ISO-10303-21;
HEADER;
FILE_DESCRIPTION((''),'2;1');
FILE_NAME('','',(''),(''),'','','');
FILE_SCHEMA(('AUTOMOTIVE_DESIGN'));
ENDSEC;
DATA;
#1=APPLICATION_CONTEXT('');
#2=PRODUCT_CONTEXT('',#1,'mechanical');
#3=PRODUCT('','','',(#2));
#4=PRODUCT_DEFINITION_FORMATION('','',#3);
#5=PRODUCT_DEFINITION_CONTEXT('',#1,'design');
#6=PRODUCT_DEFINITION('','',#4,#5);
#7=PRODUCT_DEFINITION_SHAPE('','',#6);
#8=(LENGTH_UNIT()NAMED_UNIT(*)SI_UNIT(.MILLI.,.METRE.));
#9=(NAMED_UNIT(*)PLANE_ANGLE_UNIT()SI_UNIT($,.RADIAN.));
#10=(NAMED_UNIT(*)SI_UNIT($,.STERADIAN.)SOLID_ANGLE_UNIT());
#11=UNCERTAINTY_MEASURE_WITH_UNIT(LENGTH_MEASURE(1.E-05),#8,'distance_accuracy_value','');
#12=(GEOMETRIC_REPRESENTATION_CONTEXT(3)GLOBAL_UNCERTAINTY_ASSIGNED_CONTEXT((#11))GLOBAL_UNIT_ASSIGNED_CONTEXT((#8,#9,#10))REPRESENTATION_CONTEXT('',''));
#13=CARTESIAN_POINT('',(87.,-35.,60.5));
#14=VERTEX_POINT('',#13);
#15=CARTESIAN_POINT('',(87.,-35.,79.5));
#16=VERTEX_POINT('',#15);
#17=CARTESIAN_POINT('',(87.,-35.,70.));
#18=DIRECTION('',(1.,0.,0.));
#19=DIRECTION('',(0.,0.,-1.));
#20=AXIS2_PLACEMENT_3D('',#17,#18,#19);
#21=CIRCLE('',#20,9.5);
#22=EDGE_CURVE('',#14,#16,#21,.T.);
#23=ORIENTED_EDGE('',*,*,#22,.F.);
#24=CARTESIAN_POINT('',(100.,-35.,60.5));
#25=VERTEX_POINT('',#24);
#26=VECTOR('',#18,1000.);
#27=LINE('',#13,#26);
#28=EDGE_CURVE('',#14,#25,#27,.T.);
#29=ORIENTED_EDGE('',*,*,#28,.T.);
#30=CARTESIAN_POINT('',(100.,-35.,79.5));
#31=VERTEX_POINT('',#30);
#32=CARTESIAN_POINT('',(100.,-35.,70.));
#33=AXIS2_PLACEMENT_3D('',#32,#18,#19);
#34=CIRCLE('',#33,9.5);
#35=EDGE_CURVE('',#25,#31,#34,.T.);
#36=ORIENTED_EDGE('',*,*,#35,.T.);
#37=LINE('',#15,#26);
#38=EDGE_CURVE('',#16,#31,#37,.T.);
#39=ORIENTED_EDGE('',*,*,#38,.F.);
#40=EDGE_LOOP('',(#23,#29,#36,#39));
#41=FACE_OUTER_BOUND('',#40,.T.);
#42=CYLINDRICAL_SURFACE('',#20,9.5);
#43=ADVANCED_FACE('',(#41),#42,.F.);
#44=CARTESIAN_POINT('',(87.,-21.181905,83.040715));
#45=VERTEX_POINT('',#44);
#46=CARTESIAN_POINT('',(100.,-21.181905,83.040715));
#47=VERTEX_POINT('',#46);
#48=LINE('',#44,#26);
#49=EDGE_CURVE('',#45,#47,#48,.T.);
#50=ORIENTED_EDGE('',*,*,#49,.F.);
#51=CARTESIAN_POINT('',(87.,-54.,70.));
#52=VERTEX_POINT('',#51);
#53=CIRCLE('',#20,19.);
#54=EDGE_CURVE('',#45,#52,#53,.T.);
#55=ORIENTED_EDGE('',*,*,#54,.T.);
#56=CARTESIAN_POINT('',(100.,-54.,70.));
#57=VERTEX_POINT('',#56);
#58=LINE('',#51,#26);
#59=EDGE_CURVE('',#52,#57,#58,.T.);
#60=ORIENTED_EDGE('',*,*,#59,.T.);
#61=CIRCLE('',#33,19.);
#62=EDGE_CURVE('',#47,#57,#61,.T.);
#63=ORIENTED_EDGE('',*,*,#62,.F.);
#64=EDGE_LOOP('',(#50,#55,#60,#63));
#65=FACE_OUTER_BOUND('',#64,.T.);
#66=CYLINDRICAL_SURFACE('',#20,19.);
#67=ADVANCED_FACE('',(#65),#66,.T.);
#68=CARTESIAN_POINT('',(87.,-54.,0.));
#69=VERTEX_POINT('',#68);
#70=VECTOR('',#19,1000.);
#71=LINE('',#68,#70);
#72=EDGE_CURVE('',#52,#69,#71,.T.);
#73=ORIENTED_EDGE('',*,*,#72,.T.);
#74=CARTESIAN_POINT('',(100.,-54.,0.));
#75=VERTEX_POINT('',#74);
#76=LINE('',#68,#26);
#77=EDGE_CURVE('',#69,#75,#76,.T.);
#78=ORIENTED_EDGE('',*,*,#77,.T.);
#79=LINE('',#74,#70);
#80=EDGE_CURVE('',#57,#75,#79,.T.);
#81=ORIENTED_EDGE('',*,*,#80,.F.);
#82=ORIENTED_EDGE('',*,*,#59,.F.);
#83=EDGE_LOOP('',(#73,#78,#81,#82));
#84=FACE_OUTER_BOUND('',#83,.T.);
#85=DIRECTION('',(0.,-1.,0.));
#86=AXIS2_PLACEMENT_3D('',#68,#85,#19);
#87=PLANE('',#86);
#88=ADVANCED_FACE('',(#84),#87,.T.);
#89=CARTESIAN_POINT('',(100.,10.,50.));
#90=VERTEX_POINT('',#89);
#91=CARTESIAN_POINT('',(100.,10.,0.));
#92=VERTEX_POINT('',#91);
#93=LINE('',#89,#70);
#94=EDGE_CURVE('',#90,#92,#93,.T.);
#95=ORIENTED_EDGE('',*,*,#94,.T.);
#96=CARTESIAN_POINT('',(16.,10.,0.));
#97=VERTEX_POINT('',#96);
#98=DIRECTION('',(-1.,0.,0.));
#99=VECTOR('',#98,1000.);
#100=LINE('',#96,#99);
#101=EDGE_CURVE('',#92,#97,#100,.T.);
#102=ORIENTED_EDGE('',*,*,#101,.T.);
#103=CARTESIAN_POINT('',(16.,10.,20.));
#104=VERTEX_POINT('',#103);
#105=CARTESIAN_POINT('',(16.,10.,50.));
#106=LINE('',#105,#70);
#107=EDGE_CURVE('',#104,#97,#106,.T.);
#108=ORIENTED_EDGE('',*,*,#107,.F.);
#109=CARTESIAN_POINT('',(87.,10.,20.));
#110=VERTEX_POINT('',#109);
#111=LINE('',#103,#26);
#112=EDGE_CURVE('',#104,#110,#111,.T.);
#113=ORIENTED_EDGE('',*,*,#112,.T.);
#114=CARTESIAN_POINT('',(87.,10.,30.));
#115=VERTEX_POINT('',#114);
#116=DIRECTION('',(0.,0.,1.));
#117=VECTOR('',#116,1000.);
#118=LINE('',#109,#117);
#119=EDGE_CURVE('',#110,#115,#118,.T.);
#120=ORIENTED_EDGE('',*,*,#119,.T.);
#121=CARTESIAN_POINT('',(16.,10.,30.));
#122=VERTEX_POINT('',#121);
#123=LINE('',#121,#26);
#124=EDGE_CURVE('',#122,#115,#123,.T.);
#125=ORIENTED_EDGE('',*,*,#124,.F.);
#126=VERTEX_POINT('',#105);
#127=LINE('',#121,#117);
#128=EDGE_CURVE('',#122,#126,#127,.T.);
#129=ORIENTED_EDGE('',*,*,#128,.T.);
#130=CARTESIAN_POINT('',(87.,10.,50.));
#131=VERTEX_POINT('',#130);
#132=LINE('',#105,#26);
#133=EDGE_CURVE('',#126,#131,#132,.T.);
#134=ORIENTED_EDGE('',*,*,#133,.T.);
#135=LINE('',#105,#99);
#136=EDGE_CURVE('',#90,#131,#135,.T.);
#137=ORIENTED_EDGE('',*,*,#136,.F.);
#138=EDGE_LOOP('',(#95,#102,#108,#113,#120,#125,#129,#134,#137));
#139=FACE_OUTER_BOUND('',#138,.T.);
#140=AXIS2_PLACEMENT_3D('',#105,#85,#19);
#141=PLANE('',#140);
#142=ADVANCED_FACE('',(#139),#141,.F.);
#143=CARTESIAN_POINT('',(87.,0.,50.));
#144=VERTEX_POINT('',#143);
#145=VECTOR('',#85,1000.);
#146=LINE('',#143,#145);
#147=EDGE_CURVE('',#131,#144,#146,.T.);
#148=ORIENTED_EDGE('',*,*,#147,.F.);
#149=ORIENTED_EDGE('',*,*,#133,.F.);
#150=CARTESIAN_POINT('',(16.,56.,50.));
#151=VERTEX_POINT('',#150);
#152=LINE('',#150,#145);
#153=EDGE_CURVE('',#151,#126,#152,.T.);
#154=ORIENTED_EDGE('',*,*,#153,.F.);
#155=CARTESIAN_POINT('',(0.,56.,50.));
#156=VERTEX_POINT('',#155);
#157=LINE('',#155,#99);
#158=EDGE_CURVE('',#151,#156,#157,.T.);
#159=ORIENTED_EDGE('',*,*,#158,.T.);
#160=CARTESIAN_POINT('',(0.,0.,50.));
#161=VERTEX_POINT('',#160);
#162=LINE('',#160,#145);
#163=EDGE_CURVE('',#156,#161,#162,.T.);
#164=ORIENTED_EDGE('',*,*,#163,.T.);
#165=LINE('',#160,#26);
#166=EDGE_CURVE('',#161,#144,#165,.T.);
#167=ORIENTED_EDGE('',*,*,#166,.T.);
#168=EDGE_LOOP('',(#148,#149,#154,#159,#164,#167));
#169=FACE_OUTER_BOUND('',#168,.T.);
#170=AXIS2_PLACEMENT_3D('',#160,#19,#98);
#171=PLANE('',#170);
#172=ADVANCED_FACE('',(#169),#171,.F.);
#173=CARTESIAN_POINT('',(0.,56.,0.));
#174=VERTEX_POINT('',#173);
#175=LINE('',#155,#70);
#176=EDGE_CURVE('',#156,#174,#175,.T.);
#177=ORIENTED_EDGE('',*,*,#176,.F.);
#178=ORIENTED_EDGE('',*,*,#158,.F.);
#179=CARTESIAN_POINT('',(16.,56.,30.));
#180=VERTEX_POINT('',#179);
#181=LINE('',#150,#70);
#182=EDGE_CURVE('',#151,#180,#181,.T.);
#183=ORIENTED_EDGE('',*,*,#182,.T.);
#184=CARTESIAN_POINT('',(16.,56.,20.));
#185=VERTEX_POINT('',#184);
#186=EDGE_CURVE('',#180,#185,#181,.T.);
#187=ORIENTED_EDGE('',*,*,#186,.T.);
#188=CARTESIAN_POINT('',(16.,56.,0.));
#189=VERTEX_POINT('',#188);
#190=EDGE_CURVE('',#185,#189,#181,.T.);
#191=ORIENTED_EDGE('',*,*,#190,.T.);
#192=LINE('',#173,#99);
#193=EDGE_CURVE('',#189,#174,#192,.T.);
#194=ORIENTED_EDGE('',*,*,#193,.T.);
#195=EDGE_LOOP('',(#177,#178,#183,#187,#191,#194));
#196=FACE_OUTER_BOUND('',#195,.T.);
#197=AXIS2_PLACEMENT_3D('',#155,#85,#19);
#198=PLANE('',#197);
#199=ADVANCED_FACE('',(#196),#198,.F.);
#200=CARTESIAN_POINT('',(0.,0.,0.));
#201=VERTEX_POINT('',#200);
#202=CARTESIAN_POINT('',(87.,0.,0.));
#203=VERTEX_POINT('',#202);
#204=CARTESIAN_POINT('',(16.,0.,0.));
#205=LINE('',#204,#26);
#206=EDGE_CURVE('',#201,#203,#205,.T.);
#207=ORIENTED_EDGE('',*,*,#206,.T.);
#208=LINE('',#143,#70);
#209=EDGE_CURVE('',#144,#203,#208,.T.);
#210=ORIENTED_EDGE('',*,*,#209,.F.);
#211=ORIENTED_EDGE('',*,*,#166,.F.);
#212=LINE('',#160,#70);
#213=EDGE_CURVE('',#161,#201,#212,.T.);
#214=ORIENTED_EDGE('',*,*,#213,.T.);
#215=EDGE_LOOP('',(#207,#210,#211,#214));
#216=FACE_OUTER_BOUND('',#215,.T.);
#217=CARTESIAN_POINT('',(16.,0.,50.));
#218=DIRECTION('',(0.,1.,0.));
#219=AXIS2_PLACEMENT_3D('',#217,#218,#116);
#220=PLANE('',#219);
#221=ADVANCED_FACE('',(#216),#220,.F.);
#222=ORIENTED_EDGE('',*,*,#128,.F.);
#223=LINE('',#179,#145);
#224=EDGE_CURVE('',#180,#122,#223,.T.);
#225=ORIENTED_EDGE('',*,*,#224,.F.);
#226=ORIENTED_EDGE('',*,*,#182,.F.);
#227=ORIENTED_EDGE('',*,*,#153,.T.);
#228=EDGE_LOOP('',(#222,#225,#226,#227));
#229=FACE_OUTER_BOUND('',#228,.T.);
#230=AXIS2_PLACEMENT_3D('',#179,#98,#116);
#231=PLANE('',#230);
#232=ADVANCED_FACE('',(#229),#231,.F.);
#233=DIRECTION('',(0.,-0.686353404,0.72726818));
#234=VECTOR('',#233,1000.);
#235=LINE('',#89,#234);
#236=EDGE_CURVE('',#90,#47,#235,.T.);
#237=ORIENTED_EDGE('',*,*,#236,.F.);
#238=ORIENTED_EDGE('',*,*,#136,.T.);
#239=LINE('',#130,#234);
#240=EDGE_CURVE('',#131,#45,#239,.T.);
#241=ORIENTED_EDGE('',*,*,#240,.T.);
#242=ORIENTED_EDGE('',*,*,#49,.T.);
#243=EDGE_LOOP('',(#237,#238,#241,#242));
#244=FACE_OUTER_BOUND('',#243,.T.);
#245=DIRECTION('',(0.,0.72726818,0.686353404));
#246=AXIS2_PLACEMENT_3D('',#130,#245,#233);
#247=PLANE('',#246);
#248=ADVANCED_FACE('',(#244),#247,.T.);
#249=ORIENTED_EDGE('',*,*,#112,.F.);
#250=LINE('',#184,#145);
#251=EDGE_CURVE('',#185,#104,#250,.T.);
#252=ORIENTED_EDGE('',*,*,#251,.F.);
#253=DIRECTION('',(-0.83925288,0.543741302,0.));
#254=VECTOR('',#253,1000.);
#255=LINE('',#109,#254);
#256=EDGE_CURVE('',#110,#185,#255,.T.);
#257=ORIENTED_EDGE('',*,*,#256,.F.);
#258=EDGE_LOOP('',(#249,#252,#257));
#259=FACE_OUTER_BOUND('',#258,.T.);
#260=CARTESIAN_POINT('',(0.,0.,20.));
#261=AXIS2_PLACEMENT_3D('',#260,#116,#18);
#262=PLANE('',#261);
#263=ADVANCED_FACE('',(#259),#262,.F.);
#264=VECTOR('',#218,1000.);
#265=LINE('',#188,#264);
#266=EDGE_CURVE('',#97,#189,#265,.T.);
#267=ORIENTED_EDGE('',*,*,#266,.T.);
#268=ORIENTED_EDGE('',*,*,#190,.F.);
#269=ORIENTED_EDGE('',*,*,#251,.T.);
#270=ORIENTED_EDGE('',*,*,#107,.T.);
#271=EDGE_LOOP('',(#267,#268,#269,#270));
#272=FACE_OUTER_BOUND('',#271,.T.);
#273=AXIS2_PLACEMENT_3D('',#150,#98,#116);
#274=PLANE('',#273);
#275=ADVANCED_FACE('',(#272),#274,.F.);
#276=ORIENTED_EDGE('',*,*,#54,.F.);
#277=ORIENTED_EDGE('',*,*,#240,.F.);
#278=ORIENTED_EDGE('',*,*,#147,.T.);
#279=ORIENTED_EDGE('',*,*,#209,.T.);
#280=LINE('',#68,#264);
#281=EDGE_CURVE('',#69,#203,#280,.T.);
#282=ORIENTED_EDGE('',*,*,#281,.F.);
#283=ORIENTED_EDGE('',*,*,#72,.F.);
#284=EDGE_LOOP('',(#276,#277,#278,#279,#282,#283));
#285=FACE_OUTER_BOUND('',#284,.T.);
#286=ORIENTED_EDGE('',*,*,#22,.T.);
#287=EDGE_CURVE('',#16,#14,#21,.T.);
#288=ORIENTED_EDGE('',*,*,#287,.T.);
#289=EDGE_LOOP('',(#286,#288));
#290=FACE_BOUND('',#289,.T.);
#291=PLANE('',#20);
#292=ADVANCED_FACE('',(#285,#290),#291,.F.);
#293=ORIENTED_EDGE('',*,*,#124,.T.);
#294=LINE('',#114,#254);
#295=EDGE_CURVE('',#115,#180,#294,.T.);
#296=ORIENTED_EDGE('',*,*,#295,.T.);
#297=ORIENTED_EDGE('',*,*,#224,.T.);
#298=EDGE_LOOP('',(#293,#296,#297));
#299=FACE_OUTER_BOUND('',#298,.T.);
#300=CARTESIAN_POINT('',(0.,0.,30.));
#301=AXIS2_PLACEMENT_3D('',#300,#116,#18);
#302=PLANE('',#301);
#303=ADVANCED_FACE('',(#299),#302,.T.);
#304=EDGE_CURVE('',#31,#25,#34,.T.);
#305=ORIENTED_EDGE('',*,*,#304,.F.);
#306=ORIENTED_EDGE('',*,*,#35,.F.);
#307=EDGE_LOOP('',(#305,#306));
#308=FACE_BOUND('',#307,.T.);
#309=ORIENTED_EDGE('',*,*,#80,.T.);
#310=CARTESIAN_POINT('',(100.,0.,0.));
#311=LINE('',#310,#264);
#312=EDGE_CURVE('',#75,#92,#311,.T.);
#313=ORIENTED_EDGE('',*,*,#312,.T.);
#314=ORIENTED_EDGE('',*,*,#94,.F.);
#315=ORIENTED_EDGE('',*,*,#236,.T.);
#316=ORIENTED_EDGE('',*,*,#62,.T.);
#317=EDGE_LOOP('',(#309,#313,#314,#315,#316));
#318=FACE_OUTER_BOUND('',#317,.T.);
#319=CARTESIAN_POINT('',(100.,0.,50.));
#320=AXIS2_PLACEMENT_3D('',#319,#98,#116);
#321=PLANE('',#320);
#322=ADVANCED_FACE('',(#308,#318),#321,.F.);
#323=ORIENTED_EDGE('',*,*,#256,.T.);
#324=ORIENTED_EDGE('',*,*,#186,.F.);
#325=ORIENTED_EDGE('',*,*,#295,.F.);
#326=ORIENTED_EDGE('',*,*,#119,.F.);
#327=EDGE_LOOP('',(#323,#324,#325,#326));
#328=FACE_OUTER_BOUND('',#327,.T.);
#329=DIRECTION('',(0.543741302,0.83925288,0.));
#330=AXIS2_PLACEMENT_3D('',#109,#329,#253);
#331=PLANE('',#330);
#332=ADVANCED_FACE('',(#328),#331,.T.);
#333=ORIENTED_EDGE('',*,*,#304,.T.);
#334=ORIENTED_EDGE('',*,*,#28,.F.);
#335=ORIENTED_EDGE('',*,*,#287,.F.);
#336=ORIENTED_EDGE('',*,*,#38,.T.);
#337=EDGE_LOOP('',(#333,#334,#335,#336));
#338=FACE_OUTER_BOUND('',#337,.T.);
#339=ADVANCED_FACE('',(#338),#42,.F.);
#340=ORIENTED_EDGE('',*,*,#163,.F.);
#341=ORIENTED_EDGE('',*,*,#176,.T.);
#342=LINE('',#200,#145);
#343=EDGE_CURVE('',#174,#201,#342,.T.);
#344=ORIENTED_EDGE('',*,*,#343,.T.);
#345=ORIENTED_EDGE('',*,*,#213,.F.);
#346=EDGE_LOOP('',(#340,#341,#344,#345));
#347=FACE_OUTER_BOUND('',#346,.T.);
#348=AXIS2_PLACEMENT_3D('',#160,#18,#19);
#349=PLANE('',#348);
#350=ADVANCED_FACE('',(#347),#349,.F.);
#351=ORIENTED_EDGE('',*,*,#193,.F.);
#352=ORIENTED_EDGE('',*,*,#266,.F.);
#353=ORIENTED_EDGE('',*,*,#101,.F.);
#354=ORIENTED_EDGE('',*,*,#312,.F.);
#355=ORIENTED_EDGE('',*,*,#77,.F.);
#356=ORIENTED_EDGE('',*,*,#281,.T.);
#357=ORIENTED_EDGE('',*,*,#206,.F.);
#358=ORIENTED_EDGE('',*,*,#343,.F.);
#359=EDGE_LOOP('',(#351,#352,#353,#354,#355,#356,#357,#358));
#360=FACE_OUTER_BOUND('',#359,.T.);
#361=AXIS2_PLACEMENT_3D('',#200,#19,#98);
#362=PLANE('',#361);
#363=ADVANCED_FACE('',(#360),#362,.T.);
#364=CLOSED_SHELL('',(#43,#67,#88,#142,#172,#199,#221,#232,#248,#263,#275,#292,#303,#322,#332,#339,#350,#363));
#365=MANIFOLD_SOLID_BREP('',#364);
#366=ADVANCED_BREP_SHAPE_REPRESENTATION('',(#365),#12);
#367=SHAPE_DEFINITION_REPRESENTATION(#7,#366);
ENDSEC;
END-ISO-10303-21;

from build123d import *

# Parameters (mm, degrees)
BASE_BRACKET_DEPTH    = 50
PIVOT_LUG_DEPTH       = 13
PIVOT_HOLE_SKETCH_R   = 9.5
PIVOT_HOLE_19_DEPTH   = 13
GUSSET_DEPTH          = 30
GUSSET_TRIM_CUT_DEPTH = 20


with BuildPart() as part:
    # Base Profile Sketch → Base Bracket (new body)
    with BuildSketch(Plane.XY):
        Polygon((0, 0), (16, 0), (100, 0), (100, 10), (16, 10), (16, 56), (0, 56), align=None)
    extrude(amount=BASE_BRACKET_DEPTH)

    # Pivot Lug Sketch → Pivot Lug (add)
    with BuildSketch(Plane(origin=(100, 0, 0), x_dir=(0, 0, -1), z_dir=(1, 0, 0))):
        with BuildLine():
            Line((0, -54), (0, 10))
            Line((0, 10), (-50, 10))
            Line((-50, 10), (-83.040714674, -21.181904589))
            ThreePointArc((-83.040714674, -21.181904589), (-87.657063924, -42.016273484), (-70, -54))
            Line((-70, -54), (0, -54))
        make_face()
    extrude(amount=-PIVOT_LUG_DEPTH)

    # Pivot Hole Sketch → Pivot Hole Ø19 (cut)
    with BuildSketch(Plane(origin=(100, 0, 0), x_dir=(0, 0, -1), z_dir=(1, 0, 0))):
        with Locations((-70, -35)):
            Circle(PIVOT_HOLE_SKETCH_R)
    extrude(amount=-PIVOT_HOLE_19_DEPTH, mode=Mode.SUBTRACT)

    # Gusset Sketch → Gusset (add)
    with BuildSketch(Plane.XY.offset(50)):
        Polygon((16, 56), (16, 10), (87, 10), align=None)
    extrude(amount=-GUSSET_DEPTH)

    # Gusset Trim Sketch → Gusset Trim Cut (cut)
    with BuildSketch(Plane.XY.offset(50)):
        Polygon((16, 56), (16, 10), (87, 10), align=None)
    extrude(amount=-GUSSET_TRIM_CUT_DEPTH, mode=Mode.SUBTRACT)


solid = part.part
